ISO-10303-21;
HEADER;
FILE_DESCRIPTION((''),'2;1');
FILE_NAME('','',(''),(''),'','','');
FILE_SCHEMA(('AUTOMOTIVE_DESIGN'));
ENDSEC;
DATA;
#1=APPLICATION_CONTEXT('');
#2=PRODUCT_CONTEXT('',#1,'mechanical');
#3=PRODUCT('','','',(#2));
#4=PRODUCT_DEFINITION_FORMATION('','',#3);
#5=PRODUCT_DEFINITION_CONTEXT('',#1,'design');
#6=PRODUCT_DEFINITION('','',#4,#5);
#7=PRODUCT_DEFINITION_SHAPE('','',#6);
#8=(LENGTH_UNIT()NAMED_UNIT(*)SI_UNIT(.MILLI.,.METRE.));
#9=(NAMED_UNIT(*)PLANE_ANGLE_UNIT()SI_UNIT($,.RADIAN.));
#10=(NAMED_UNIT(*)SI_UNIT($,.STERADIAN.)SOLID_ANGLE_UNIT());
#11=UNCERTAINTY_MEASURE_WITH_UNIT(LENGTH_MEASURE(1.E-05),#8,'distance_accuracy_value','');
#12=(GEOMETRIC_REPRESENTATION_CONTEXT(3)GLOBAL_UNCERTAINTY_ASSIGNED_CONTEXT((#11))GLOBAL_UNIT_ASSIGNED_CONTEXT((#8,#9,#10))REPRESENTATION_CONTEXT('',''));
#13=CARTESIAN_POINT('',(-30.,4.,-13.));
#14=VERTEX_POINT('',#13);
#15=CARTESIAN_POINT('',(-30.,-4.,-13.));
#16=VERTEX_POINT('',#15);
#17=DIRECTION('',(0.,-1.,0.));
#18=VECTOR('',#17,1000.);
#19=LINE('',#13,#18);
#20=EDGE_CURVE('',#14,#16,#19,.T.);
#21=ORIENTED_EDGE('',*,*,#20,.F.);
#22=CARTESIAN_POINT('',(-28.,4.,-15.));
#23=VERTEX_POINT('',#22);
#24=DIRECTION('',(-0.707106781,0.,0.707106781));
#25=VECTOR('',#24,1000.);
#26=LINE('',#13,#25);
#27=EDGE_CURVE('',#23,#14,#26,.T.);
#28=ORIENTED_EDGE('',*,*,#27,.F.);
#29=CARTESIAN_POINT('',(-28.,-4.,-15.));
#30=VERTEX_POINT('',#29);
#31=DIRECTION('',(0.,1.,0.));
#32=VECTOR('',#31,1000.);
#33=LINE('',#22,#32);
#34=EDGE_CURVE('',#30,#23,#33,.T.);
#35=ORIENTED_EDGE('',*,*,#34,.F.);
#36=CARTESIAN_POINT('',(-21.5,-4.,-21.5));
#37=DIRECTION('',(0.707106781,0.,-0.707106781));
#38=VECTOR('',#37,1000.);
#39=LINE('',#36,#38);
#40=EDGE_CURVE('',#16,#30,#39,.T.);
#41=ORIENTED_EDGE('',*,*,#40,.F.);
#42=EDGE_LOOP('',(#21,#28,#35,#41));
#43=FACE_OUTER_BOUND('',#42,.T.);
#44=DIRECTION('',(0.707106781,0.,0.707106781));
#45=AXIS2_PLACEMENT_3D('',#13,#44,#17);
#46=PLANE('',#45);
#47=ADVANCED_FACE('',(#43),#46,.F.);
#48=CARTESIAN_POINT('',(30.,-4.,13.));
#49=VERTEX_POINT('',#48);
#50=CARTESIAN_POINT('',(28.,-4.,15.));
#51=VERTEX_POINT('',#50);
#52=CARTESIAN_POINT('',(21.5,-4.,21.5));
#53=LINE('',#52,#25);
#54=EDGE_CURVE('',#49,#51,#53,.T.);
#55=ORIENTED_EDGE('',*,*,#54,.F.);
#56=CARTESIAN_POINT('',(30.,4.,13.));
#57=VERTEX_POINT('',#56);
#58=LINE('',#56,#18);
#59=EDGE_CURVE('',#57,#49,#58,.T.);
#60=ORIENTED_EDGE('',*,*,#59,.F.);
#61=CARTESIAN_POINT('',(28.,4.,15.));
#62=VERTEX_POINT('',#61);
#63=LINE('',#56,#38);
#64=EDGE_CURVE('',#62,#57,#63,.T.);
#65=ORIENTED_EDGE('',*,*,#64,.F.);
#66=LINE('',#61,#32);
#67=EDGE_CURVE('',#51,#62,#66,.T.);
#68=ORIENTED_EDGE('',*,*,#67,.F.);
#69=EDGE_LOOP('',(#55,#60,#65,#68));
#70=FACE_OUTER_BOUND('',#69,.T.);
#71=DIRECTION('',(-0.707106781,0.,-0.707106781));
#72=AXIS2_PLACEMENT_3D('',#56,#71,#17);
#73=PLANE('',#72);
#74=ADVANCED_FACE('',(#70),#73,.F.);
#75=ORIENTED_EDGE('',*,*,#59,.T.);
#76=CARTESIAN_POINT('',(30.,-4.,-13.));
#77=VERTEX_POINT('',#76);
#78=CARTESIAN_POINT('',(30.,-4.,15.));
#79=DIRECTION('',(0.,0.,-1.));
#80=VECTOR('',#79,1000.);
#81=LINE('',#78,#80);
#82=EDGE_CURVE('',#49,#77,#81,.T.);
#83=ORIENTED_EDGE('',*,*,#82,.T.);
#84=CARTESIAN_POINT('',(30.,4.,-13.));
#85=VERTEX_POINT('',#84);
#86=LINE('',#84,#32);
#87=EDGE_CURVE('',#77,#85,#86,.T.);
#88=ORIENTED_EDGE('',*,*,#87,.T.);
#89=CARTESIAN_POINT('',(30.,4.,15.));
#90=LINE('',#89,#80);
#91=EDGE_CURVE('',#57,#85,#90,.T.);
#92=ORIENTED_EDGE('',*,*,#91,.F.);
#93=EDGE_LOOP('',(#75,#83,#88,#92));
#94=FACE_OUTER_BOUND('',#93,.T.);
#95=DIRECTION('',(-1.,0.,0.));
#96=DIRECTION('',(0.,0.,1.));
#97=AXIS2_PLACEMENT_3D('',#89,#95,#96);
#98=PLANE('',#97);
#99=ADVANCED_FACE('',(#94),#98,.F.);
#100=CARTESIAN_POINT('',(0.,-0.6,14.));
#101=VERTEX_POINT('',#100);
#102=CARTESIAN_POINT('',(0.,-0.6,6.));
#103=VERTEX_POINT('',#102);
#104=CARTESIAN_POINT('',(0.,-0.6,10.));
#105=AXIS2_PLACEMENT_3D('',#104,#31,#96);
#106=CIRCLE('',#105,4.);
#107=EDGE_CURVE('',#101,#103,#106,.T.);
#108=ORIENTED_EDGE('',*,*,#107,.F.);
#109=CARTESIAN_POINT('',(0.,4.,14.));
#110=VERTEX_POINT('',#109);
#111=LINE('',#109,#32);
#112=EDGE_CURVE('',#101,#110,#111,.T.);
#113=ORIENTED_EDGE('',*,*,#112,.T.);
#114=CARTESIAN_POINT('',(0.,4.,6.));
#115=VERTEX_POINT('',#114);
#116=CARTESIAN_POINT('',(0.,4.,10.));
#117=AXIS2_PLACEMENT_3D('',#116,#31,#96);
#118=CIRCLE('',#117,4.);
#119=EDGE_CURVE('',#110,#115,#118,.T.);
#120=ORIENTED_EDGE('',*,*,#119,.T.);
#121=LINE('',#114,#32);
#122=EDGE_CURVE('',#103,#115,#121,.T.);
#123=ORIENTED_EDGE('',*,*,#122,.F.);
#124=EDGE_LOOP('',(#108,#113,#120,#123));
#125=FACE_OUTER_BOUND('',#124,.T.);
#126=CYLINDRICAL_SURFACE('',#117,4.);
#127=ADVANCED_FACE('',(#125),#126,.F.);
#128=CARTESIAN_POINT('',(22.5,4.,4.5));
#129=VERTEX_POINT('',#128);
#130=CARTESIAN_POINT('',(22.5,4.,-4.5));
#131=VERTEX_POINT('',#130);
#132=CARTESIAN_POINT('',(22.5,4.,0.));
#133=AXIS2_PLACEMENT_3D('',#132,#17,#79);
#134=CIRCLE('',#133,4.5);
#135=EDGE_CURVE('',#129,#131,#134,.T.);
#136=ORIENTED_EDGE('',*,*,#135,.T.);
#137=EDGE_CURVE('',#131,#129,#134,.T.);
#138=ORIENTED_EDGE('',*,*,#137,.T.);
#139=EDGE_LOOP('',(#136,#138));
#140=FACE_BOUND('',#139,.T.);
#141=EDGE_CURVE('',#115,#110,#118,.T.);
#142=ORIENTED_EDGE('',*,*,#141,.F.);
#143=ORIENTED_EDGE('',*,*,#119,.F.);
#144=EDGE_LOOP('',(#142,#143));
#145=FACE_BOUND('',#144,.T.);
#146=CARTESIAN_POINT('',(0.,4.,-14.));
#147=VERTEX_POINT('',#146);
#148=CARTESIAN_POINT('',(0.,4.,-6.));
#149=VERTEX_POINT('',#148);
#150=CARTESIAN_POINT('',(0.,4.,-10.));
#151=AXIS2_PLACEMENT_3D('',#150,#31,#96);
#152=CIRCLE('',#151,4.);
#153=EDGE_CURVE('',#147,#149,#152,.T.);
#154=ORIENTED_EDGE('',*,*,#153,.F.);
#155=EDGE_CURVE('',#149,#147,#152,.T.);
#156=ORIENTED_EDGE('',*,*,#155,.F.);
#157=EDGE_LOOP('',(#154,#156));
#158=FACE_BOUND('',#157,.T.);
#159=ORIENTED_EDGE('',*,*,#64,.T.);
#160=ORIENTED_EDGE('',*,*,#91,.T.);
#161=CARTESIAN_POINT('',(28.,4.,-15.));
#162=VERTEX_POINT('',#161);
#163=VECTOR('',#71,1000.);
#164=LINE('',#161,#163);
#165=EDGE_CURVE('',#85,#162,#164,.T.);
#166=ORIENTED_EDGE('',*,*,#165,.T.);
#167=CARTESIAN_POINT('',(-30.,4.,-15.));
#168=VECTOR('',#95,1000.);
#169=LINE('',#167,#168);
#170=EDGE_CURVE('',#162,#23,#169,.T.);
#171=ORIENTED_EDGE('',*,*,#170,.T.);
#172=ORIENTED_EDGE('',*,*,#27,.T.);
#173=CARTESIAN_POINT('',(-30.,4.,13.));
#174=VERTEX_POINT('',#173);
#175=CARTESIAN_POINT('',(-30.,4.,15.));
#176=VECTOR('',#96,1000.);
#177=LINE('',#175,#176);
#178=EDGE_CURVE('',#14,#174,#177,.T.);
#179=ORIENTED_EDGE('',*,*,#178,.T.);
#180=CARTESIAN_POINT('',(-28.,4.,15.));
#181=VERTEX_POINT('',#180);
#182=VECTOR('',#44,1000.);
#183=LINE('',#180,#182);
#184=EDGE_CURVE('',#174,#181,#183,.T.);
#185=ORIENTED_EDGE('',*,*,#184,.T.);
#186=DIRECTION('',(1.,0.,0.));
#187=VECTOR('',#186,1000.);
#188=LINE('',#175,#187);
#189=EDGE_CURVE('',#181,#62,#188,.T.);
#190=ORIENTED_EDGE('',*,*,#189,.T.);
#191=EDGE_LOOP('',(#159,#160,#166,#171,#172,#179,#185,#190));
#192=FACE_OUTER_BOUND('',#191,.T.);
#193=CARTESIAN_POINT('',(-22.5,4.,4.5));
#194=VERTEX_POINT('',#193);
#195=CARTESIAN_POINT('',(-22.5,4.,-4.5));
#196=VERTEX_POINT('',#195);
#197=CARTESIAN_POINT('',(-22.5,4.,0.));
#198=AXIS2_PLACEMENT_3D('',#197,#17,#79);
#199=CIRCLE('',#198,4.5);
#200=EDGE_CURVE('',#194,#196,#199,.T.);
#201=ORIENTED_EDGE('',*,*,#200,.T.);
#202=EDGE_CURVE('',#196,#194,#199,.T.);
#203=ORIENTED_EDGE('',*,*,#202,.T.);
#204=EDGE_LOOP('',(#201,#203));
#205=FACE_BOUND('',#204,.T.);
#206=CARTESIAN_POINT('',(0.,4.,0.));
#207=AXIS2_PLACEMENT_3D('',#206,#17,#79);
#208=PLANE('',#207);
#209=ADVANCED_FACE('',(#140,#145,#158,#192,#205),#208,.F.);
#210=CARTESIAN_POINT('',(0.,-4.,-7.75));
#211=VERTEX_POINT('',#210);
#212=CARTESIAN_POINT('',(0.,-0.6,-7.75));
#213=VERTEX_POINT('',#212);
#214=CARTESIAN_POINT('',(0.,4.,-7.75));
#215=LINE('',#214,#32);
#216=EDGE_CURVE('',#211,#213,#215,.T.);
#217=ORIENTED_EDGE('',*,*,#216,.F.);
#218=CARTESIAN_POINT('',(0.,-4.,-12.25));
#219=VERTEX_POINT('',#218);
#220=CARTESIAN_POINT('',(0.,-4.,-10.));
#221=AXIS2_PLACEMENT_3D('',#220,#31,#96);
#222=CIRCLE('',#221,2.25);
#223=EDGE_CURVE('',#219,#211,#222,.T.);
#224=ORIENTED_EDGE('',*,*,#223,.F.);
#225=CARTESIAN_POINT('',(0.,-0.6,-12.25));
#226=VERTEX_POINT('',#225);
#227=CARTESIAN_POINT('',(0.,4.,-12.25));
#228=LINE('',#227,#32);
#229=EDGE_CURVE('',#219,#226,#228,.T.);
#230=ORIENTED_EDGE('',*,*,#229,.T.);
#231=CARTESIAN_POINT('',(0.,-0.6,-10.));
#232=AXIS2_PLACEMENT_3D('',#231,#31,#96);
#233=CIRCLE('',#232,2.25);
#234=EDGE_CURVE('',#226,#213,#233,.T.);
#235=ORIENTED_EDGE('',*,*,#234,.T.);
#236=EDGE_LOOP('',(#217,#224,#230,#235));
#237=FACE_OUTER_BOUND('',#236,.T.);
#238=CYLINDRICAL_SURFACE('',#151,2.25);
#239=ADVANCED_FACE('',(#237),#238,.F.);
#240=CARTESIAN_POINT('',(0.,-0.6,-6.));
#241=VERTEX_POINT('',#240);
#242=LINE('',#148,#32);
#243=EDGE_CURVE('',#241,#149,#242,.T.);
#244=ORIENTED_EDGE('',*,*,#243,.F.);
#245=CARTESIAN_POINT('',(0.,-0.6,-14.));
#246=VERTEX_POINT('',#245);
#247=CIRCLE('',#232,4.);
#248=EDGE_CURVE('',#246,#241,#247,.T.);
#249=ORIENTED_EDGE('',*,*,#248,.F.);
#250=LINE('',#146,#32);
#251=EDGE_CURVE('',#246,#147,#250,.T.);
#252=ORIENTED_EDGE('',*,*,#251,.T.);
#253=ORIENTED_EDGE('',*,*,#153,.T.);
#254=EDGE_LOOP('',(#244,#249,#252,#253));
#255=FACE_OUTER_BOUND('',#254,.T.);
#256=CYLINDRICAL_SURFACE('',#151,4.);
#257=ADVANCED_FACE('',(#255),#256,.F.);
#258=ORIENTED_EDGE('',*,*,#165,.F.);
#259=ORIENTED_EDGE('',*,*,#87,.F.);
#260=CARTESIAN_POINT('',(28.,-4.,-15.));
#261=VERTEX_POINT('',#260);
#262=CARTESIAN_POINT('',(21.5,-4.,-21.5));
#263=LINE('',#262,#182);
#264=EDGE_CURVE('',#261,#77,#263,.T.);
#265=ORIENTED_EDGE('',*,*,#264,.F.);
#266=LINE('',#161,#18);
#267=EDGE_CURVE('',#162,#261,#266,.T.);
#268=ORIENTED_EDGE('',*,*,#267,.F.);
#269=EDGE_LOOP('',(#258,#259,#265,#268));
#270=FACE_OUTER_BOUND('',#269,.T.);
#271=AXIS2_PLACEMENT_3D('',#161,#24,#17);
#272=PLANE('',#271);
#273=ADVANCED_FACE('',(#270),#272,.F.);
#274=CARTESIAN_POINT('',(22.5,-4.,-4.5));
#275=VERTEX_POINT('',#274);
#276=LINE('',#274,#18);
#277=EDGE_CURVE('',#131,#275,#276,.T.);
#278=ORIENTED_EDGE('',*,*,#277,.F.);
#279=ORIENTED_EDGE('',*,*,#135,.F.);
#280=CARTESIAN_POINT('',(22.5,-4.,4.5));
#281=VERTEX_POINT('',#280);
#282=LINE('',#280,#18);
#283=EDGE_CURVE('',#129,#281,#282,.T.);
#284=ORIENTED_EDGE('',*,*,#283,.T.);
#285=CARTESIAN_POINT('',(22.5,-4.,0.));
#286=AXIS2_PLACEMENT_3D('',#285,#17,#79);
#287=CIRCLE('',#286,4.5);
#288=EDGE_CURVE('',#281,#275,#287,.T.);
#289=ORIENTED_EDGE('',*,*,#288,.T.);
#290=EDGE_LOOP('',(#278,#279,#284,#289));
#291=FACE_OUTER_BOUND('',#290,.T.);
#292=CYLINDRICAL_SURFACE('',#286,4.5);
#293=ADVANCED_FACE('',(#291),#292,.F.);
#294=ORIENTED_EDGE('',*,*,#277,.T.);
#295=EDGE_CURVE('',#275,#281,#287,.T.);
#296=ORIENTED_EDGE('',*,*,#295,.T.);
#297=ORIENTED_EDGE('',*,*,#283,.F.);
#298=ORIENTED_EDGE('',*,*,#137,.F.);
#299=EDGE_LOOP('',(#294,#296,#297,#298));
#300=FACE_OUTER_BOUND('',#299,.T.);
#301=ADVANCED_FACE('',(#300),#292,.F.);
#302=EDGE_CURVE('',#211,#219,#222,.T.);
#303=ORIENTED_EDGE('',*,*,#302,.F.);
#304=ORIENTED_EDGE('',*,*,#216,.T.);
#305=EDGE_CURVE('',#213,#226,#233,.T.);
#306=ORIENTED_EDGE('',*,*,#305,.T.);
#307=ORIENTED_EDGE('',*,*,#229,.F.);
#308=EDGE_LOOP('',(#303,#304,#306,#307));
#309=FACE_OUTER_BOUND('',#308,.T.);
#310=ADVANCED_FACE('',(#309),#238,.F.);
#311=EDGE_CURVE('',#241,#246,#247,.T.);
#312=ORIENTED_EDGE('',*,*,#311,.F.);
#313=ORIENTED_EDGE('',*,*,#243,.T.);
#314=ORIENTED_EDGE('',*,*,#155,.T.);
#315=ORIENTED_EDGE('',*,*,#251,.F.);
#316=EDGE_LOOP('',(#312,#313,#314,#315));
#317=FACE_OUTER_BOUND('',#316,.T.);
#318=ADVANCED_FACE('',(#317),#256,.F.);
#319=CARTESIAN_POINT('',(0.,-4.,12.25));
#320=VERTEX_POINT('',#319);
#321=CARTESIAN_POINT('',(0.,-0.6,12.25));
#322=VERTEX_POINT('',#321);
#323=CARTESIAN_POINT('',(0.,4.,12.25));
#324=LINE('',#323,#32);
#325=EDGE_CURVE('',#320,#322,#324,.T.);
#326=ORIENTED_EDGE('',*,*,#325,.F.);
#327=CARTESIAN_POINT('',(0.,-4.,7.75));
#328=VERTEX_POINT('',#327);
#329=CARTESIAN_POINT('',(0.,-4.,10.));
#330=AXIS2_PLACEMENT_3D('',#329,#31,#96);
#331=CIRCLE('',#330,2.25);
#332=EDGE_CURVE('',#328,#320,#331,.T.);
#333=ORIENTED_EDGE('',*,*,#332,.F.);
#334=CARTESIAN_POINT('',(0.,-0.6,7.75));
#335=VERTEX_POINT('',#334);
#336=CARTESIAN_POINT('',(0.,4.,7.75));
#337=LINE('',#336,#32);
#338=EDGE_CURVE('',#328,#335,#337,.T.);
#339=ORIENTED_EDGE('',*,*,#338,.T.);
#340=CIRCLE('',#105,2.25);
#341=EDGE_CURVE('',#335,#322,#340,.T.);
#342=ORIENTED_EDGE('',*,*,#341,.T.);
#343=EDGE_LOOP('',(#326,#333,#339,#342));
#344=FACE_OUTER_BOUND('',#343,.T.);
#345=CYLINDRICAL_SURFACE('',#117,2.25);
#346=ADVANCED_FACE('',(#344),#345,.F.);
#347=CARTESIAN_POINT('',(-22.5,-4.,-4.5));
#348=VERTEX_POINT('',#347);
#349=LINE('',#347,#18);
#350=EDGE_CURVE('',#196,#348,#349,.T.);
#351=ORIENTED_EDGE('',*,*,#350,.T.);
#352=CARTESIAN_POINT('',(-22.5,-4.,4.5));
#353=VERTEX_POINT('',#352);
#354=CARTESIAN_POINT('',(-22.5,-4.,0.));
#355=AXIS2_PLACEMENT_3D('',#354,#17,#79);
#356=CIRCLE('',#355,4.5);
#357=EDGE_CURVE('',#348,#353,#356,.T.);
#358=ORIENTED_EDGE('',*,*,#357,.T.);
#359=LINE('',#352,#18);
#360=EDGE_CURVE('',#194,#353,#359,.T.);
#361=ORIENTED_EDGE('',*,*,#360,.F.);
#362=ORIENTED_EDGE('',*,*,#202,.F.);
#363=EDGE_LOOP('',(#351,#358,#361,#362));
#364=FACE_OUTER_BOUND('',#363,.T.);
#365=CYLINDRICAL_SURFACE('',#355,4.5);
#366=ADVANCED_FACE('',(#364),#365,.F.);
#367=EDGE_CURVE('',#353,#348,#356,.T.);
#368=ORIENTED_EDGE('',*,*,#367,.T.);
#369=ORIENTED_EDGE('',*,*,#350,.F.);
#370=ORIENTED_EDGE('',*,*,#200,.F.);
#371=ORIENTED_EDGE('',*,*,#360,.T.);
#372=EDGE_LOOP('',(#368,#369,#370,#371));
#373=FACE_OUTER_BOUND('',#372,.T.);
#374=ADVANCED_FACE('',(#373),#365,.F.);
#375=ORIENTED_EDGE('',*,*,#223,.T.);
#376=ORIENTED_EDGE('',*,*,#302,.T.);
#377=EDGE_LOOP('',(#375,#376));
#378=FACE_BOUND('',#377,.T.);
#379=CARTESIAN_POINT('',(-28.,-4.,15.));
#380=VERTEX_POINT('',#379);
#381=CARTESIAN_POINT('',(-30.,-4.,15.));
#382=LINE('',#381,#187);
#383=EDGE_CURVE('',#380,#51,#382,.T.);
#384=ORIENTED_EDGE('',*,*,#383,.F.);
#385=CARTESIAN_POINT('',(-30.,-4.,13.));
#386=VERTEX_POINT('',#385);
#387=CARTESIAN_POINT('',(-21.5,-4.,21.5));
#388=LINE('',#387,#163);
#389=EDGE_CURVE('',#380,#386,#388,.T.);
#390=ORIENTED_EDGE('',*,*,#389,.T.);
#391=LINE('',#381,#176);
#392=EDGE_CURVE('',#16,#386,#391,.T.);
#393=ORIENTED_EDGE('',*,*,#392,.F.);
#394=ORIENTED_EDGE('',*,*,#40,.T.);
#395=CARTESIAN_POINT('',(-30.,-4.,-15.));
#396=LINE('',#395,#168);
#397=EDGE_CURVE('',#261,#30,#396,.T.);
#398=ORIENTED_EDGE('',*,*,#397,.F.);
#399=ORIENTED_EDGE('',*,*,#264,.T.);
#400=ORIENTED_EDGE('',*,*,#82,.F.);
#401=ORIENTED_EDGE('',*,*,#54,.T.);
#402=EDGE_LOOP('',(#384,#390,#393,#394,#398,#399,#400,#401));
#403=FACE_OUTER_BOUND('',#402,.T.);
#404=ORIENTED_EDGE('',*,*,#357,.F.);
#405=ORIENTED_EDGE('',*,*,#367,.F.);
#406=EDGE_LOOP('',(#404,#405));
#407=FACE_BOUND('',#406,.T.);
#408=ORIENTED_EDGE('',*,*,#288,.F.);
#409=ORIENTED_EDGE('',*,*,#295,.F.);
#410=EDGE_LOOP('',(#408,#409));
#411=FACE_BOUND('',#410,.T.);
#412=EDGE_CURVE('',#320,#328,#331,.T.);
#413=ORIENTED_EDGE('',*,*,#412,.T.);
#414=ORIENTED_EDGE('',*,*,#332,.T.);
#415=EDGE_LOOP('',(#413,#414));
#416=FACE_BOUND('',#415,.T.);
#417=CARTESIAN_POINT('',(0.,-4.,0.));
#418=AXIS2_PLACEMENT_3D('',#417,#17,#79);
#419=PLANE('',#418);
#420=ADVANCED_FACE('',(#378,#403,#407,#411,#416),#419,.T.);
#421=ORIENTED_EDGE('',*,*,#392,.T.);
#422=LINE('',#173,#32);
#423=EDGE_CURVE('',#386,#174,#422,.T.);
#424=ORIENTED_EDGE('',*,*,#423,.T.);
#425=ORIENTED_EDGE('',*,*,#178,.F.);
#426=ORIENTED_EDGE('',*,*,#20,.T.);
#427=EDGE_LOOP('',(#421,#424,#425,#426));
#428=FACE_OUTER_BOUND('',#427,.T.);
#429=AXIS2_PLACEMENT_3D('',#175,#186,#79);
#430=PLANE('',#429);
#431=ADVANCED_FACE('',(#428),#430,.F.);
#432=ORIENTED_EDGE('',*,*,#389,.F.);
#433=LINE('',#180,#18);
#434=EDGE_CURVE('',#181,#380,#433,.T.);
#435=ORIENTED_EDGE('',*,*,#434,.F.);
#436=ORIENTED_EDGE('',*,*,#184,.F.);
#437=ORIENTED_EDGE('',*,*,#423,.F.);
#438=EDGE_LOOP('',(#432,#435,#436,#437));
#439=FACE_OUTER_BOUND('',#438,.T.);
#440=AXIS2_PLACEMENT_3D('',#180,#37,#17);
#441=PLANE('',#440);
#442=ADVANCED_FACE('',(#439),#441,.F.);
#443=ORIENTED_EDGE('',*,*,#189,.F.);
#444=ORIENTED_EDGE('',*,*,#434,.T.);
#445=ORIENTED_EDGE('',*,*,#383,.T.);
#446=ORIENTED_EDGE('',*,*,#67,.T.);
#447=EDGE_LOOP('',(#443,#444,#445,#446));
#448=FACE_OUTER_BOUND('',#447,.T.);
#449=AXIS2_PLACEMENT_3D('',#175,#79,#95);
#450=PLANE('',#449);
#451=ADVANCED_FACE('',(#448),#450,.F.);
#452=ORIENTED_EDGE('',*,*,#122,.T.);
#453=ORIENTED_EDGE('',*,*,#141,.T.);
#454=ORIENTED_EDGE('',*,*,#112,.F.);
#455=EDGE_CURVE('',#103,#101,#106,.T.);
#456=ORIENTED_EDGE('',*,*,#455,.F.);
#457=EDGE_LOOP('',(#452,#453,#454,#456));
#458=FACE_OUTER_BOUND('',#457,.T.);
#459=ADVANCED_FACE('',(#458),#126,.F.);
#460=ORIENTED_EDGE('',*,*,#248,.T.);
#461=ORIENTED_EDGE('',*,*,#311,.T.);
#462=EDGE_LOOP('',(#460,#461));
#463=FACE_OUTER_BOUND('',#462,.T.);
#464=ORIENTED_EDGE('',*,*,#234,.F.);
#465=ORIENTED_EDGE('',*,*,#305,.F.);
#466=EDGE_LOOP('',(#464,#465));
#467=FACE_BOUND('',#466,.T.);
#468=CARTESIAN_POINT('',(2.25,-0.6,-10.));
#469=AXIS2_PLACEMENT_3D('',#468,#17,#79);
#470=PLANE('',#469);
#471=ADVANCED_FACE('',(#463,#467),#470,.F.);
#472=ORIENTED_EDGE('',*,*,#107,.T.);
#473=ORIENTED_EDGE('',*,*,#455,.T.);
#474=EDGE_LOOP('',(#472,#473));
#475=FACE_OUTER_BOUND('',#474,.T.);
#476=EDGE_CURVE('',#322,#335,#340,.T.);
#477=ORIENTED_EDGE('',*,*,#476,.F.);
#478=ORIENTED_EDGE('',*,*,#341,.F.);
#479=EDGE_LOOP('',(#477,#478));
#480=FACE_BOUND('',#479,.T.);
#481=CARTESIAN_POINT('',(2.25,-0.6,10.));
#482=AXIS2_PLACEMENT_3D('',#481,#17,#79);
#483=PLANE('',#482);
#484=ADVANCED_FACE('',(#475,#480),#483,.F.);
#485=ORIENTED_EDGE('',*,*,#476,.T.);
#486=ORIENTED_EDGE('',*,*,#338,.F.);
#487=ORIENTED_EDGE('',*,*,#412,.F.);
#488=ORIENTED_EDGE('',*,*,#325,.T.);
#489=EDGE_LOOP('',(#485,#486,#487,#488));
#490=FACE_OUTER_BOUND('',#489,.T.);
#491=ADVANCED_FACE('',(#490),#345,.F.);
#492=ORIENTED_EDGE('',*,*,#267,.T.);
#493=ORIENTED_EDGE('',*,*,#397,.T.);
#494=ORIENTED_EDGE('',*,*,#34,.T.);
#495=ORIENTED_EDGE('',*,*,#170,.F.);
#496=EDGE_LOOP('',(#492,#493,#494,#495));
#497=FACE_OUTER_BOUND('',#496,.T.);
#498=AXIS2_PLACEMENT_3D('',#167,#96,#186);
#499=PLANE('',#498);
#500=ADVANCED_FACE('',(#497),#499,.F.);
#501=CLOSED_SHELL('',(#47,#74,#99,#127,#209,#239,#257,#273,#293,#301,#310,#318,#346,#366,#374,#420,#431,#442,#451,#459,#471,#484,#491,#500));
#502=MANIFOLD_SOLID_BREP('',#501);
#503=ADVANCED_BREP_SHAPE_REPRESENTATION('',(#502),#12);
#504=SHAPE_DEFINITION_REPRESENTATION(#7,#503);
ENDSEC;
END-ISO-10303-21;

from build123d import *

# Parameters (mm, degrees)
SKETCH_1_W                = 60
SKETCH_1_H                = 30
EXTRUDE_1_DEPTH           = 4
CHAMFER_1_SIZE            = 2
HOLE_WIZARD_1_D           = 4.5
HOLE_WIZARD_1_CBORE_D     = 8
HOLE_WIZARD_1_CBORE_DEPTH = 4.6
M10X1_0_1_D               = 9


with BuildPart() as part:
    # 草图1 → 凸台-拉伸1 (new, symmetric)
    with BuildSketch(Plane(origin=(0, 0, 0), x_dir=(1, 0, 0), z_dir=(0, 1, 0))):
        Rectangle(SKETCH_1_W, SKETCH_1_H)
    extrude(amount=EXTRUDE_1_DEPTH, both=True)

    # 倒角1
    chamfer_1_edges = [part.edges().sort_by_distance(p)[0] for p in [
        (30, 0, 15),
        (-30, 0, 15),
        (-30, 0, -15),
        (30, 0, -15),
    ]]
    chamfer(chamfer_1_edges, length=CHAMFER_1_SIZE)

    # 打孔尺寸(%根据)内六角圆柱头螺钉的类型1 (through all)
    with Locations(Plane(origin=(0, 4, 0), x_dir=(1, 0, 0), z_dir=(0, 1, 0))):
        with Locations((0, -10), (0, 10)):
            CounterBoreHole(HOLE_WIZARD_1_D / 2, HOLE_WIZARD_1_CBORE_D / 2, HOLE_WIZARD_1_CBORE_DEPTH)

    # M10x1.0 螺纹孔1 (through all)
    with Locations(Plane(origin=(0, -4, 0), x_dir=(-1, 0, 0), z_dir=(0, -1, 0))):
        with Locations((-22.5, 0), (22.5, 0)):
            Hole(M10X1_0_1_D / 2)


solid = part.part
